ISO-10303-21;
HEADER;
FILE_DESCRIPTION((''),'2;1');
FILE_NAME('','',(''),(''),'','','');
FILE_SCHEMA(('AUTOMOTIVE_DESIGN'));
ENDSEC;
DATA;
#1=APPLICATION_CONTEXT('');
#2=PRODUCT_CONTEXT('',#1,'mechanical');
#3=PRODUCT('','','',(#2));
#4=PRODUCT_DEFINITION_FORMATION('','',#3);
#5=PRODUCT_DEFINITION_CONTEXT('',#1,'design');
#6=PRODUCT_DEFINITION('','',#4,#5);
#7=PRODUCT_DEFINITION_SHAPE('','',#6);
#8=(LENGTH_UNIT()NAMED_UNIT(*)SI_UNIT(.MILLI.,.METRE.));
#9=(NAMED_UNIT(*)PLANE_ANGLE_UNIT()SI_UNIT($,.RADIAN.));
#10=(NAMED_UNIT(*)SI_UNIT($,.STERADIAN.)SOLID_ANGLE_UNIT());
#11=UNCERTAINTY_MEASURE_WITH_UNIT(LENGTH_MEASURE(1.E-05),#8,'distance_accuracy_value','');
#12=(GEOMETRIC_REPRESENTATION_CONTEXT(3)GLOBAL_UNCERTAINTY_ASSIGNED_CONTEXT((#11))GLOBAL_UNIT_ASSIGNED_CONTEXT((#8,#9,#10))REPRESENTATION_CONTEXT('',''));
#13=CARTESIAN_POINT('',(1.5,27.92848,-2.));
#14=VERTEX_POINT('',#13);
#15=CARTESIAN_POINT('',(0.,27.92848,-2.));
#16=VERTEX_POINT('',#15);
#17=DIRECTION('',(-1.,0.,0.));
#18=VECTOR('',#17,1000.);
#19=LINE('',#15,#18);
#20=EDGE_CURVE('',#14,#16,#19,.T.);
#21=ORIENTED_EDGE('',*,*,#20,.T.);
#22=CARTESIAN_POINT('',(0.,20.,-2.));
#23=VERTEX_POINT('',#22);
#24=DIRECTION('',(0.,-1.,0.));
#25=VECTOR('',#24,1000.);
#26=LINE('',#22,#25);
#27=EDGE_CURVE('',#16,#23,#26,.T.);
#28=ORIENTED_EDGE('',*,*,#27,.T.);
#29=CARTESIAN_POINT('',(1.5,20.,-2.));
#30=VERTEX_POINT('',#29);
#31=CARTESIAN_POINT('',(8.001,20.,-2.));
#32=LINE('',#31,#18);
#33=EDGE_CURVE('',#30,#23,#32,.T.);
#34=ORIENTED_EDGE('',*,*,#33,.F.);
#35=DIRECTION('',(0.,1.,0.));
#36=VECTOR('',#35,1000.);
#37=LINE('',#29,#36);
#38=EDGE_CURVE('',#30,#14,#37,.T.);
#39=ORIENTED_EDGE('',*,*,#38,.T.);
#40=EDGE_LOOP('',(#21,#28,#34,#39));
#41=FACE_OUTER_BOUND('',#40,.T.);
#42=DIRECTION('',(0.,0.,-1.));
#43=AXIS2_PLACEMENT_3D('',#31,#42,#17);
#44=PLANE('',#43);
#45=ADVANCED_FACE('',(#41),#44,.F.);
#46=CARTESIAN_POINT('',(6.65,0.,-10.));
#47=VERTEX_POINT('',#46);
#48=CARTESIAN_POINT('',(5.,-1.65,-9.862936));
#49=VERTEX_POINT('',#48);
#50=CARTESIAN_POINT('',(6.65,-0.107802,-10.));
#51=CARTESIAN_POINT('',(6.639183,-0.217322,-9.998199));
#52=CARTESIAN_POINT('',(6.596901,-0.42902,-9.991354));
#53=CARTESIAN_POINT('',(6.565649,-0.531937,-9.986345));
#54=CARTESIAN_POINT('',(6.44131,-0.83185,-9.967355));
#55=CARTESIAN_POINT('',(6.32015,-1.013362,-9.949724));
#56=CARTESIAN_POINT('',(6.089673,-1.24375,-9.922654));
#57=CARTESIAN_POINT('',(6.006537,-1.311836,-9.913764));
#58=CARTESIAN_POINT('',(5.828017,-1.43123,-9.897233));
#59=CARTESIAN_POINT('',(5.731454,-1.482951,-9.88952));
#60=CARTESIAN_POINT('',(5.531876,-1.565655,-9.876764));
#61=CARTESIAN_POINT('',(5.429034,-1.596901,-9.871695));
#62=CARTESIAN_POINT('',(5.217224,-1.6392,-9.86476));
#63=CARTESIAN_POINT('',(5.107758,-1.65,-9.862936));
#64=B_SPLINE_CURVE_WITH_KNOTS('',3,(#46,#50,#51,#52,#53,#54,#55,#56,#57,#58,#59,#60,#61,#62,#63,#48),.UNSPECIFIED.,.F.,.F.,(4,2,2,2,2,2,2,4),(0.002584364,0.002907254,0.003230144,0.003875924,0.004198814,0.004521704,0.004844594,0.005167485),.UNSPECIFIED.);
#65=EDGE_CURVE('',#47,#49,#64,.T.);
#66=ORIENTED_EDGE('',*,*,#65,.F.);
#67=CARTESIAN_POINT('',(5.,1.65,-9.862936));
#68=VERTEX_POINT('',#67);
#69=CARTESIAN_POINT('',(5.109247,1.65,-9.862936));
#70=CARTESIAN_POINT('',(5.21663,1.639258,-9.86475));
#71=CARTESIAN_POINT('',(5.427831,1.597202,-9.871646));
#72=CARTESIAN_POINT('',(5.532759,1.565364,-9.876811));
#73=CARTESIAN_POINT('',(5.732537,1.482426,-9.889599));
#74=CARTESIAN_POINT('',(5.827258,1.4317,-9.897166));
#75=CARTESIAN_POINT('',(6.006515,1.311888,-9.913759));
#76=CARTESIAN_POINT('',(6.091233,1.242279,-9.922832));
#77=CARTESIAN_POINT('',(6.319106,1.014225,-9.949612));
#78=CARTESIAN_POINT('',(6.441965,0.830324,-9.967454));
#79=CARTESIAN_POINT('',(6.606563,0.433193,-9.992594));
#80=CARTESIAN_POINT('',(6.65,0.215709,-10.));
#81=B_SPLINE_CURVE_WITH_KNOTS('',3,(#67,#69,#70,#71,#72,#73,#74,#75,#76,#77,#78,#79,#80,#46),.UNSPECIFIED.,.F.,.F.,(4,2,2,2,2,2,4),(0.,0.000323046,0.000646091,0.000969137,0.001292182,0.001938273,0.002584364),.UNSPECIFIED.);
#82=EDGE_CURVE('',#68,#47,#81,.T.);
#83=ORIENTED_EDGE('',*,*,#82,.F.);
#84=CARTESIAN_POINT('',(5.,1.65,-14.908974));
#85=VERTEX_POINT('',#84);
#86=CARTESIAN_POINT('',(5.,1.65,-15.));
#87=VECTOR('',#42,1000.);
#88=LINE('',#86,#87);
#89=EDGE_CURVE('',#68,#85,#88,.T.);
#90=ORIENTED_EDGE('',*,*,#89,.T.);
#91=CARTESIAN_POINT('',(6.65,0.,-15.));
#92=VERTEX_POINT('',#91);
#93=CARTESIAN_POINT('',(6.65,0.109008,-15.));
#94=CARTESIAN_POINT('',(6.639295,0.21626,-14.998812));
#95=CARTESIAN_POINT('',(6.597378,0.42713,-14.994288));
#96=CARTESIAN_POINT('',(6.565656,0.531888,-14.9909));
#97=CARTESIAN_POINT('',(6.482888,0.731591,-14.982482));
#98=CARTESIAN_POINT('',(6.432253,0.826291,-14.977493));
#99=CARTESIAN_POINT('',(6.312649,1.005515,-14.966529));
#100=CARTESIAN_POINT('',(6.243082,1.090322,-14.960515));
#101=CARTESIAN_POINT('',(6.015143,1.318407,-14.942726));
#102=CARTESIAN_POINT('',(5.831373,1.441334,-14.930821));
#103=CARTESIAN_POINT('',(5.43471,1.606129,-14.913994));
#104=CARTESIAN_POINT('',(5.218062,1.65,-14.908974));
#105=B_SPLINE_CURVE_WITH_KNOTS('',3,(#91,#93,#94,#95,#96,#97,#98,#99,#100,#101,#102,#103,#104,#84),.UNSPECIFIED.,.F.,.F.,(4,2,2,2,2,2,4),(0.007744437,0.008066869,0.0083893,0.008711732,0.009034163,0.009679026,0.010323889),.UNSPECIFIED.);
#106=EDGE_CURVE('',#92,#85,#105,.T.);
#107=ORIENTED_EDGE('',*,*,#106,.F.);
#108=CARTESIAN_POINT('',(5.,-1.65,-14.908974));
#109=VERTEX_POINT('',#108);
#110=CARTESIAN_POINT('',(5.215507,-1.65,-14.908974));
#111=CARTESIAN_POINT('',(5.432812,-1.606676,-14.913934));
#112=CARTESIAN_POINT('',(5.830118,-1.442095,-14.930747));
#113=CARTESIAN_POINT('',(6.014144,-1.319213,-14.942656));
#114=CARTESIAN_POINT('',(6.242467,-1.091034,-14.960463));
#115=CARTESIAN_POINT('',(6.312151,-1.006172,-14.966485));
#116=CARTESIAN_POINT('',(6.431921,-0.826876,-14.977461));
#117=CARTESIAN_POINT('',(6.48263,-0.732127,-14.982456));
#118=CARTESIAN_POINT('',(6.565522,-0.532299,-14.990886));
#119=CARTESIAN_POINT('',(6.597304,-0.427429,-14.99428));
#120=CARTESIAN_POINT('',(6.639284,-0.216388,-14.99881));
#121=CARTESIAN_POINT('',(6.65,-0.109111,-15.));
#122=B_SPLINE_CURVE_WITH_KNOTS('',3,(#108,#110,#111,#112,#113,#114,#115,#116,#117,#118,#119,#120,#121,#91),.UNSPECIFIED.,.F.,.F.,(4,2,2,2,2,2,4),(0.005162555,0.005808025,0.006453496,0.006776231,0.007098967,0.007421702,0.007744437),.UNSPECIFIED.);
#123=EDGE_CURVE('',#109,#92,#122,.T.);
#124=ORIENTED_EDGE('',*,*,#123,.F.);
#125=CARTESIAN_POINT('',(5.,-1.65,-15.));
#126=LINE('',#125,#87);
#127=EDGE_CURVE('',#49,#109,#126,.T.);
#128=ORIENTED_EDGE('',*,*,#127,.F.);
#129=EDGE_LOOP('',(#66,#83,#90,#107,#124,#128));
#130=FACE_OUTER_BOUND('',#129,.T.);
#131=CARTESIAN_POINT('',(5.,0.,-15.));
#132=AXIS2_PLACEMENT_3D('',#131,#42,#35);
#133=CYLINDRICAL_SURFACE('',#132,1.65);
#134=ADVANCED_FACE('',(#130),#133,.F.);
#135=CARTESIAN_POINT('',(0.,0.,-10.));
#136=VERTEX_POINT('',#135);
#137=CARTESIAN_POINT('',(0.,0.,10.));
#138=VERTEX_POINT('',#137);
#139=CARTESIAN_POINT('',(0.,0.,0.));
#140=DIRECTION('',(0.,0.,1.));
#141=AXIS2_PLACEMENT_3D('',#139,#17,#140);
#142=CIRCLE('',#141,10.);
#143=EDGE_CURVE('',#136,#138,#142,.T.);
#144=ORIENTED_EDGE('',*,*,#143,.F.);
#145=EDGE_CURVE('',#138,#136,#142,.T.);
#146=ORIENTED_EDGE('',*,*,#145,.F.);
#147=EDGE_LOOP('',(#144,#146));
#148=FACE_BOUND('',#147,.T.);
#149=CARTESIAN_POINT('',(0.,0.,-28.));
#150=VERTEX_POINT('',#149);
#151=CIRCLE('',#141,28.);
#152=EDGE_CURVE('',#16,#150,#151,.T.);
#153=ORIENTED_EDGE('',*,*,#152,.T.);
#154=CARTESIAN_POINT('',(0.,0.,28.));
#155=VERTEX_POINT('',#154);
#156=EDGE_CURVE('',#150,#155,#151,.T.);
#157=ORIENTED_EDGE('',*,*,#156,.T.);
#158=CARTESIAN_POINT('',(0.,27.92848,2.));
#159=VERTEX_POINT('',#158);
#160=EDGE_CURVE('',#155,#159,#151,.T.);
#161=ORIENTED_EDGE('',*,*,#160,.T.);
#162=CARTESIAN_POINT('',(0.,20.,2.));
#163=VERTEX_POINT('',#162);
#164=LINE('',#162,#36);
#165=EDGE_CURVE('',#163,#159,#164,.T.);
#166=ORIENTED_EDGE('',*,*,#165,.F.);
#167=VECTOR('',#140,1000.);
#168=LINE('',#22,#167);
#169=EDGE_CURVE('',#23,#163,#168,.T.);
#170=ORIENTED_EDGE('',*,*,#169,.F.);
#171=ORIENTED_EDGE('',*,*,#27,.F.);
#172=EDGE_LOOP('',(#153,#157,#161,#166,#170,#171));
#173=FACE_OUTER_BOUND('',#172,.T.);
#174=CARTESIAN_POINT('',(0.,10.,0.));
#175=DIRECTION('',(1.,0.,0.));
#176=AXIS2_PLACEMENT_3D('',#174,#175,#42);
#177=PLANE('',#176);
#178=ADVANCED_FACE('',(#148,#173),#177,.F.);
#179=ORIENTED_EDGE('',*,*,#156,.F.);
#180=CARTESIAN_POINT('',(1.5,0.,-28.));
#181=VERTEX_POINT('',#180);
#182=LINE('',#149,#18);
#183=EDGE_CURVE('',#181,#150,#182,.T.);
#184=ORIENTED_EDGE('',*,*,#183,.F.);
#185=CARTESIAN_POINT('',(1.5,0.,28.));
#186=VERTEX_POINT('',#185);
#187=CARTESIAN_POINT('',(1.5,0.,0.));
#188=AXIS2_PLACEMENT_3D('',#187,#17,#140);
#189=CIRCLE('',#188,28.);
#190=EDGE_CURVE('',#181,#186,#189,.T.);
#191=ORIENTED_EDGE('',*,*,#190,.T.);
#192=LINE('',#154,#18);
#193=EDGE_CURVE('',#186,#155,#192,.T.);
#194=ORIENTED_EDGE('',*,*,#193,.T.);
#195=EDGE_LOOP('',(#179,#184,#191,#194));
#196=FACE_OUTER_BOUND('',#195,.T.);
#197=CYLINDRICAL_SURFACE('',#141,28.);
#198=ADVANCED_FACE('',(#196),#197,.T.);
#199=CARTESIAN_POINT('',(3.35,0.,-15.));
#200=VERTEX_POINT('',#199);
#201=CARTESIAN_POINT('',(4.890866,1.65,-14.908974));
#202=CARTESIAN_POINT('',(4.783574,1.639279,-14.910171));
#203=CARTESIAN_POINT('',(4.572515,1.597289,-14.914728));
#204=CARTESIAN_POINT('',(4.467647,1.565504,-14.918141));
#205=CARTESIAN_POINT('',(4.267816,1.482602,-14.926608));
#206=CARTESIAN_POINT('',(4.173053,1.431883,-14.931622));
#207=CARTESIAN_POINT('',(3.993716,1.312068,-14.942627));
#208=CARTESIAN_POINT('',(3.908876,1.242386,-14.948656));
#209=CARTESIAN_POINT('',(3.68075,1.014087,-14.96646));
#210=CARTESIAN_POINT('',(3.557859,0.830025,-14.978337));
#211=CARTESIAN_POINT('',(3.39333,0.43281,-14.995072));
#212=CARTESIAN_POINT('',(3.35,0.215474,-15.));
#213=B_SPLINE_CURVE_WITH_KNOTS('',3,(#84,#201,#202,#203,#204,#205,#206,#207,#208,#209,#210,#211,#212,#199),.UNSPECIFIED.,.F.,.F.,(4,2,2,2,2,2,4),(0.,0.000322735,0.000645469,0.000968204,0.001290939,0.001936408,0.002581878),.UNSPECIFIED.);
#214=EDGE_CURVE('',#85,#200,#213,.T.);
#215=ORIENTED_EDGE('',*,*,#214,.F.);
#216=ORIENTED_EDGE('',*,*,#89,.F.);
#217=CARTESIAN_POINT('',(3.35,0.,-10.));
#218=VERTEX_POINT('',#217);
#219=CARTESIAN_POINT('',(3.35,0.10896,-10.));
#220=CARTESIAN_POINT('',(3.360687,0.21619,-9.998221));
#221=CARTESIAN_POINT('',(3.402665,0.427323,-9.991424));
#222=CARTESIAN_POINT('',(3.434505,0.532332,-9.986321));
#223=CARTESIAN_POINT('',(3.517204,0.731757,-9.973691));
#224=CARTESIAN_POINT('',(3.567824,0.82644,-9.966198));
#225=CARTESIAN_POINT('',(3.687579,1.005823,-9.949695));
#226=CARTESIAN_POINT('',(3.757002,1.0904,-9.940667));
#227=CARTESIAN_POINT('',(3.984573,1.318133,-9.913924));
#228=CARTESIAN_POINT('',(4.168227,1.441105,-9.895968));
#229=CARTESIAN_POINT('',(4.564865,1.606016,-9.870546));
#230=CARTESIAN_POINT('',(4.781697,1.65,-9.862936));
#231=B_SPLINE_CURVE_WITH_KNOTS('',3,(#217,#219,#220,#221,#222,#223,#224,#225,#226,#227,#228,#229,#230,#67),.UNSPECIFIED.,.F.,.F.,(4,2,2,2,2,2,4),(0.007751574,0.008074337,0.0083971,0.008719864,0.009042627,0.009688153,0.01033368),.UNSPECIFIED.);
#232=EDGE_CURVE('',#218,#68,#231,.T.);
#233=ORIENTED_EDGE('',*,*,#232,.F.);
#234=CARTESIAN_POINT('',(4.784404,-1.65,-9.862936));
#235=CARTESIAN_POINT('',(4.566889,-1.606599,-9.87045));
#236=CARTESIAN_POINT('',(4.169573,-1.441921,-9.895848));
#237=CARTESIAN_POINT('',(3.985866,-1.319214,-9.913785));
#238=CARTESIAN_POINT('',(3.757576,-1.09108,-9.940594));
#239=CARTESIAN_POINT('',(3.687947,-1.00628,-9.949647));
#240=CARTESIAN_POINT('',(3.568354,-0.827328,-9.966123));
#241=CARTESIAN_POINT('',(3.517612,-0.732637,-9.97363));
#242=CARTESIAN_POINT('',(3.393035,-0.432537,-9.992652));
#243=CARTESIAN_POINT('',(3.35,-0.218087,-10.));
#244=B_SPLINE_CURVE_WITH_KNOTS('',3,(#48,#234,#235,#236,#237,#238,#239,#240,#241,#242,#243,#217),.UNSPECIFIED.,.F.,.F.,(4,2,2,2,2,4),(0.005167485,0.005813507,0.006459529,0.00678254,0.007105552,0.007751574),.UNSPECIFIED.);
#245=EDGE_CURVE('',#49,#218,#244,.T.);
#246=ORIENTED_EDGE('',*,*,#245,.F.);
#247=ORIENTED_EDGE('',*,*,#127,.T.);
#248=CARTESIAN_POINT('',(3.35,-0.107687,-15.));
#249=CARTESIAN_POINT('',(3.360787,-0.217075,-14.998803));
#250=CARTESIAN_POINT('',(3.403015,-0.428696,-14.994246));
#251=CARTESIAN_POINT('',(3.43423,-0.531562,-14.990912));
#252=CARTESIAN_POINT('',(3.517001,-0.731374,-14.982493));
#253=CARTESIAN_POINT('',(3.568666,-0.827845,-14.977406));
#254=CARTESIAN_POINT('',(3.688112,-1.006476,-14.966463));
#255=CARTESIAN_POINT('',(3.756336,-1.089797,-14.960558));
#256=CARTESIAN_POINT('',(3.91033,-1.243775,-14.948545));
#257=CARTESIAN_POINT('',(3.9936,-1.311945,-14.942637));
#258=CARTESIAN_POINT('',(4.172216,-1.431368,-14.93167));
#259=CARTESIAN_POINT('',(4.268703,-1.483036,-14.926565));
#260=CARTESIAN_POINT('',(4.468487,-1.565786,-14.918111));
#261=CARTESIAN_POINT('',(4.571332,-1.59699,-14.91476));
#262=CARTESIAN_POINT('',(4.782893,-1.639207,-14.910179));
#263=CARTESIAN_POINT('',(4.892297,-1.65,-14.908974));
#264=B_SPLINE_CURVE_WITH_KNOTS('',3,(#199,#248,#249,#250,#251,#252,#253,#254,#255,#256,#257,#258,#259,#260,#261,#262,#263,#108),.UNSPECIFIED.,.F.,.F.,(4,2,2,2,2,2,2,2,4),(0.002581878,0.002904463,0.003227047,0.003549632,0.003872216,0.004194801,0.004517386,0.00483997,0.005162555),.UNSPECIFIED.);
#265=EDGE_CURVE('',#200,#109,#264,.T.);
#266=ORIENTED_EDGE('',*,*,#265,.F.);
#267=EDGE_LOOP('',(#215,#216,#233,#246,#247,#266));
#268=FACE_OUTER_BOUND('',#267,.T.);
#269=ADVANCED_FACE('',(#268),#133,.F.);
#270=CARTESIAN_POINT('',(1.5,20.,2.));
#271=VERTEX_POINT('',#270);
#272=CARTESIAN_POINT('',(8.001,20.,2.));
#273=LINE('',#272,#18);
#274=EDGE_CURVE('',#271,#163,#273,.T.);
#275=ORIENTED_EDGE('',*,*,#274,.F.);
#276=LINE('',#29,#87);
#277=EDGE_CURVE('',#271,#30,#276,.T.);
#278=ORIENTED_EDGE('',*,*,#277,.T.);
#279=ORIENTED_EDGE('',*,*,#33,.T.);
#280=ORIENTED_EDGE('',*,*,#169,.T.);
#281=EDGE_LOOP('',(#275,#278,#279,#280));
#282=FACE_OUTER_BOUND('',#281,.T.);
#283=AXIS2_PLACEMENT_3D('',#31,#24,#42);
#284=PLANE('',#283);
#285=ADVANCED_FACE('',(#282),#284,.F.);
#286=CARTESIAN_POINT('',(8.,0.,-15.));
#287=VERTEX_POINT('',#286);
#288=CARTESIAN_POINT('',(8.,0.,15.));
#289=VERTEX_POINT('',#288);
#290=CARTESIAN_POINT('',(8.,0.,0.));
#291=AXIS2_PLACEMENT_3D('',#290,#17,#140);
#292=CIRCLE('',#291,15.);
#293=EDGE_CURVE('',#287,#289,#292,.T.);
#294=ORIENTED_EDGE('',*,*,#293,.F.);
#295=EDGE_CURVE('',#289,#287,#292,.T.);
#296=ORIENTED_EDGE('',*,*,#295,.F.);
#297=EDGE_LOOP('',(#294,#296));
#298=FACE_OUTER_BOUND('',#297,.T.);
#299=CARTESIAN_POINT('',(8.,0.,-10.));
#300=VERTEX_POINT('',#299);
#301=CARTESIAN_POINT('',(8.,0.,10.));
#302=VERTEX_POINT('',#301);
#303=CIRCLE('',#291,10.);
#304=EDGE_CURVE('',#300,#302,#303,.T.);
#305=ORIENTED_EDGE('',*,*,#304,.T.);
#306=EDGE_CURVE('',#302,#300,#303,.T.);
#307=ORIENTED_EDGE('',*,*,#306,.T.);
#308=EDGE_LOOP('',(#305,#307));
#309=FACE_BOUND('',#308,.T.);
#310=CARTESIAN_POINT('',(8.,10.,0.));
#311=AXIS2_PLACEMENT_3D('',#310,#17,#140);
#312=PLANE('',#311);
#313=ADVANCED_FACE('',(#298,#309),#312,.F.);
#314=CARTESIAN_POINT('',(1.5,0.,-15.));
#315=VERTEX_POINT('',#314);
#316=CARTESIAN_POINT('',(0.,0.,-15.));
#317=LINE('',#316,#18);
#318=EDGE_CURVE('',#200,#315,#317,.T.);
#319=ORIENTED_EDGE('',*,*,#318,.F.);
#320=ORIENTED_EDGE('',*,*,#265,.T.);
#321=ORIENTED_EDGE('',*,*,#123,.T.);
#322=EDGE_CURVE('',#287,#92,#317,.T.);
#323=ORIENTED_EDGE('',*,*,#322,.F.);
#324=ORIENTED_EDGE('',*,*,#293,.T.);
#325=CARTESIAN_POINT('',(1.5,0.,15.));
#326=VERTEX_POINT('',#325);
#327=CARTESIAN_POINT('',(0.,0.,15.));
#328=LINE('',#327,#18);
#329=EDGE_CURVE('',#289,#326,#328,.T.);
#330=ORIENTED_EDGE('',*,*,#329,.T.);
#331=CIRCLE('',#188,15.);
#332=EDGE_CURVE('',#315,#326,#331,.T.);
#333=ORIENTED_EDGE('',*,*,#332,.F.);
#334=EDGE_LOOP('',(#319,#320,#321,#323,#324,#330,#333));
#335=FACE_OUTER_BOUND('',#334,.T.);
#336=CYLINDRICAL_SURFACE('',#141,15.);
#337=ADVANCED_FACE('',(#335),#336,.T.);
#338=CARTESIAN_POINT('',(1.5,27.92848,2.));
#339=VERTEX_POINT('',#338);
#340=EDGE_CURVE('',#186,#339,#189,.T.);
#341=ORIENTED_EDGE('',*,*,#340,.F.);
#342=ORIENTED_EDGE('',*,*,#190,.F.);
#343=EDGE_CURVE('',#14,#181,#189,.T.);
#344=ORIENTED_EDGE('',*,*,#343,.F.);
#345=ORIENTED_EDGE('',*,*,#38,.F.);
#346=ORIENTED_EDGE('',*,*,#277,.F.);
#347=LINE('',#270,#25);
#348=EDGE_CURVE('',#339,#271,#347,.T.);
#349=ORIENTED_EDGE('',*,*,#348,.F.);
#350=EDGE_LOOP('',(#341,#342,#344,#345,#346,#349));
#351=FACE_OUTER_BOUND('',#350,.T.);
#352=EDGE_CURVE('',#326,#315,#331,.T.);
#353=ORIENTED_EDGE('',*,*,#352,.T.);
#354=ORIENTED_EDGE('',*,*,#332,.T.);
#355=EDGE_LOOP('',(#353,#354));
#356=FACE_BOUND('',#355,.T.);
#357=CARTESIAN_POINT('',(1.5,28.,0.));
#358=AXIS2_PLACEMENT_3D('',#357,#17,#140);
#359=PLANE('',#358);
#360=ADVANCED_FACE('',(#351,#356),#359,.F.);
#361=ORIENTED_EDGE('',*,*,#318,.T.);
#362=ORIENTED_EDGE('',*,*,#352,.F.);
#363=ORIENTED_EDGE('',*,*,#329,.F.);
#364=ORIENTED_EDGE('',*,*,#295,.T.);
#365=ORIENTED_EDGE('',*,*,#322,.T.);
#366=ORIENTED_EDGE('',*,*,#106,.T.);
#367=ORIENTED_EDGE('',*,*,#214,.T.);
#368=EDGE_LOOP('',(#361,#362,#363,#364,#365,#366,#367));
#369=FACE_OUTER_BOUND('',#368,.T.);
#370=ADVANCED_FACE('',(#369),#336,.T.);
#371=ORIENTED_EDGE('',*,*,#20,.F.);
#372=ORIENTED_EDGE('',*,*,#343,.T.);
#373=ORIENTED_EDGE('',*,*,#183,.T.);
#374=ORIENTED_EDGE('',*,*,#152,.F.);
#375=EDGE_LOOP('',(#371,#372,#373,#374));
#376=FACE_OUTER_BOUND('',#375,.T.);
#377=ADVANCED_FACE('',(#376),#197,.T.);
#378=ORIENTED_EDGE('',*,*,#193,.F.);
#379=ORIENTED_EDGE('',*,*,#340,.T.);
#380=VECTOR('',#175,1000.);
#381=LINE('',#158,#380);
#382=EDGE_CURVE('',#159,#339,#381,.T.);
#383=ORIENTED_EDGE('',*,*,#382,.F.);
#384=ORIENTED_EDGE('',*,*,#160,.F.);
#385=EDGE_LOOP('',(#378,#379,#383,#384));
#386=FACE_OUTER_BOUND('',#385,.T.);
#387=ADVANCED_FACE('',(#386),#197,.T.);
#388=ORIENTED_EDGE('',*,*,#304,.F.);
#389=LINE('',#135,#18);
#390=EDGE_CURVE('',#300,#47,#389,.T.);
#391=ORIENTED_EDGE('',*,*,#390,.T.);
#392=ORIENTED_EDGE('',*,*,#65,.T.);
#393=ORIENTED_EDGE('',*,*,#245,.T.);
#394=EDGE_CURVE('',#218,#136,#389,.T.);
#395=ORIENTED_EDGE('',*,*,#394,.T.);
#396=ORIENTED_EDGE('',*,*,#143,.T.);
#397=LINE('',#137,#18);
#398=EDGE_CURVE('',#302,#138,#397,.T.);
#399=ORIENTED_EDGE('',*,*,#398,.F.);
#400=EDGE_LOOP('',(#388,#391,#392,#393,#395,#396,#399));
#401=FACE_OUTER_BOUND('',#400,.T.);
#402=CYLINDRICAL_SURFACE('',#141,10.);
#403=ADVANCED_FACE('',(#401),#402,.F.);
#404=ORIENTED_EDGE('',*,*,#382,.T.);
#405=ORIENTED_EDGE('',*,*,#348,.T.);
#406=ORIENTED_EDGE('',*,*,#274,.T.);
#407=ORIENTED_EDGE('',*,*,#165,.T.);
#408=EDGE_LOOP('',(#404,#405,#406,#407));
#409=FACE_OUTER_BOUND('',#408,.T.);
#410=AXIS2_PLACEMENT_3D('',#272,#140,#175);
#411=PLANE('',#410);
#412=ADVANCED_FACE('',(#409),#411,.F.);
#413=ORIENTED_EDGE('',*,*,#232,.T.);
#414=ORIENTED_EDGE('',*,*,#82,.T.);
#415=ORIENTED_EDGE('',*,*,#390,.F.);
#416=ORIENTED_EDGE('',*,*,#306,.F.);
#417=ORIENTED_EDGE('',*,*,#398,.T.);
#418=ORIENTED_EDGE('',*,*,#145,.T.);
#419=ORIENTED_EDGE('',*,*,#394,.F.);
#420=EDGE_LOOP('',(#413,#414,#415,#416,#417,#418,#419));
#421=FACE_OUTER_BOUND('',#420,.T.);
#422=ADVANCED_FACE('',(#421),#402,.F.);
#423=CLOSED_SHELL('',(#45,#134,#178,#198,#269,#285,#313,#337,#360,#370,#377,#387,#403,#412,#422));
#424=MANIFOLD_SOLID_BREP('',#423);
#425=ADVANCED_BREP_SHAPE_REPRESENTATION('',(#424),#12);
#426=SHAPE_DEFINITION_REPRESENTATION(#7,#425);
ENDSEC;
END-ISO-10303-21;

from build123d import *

# Parameters (mm, degrees)
CUT_EXTRUDE1_REACH     = 42.398
SKETCH2_W              = 4
SKETCH2_H              = 9.816803941
M4_TAPPED_HOLE1_REACH  = 53.556
M4_TAPPED_HOLE1_BORE_R = 1.65


with BuildPart() as part:
    # Sketch1 → Revolve1 (revolve)
    with BuildSketch(Plane.XY, mode=Mode.PRIVATE) as revolve1_sk:
        Polygon((0, 10), (8, 10), (8, 15), (1.5, 15), (1.5, 28), (0, 28), align=None)
    revolve(revolve1_sk.sketch.rotate(Axis((0, 0, 0), (1, 0, 0)), 90), axis=Axis((0, 0, 0), (1, 0, 0)))

    # Sketch2 → Cut-Extrude1 (cut, up to next)
    with BuildSketch(Plane.ZY, mode=Mode.PRIVATE) as cut_extrude1_sk1:
        with Locations((0, 24.908401971)):
            Rectangle(SKETCH2_W, SKETCH2_H)
    cut_extrude1_tool1 = extrude(cut_extrude1_sk1.sketch, amount=-CUT_EXTRUDE1_REACH, mode=Mode.PRIVATE) & part.part
    add(cut_extrude1_tool1.solids().sort_by_distance((0, 24.908402, 0))[0], mode=Mode.SUBTRACT)

    # M4 Tapped Hole1 bore (on position points) → M4 Tapped Hole1 (cut, up to next)
    with BuildSketch(Plane(origin=(5, 0, -15), x_dir=(0, -1, 0), z_dir=(0, 0, -1)), mode=Mode.PRIVATE) as m4_tapped_hole1_sk1:
        Circle(M4_TAPPED_HOLE1_BORE_R)
    m4_tapped_hole1_tool1 = extrude(m4_tapped_hole1_sk1.sketch, amount=-M4_TAPPED_HOLE1_REACH, mode=Mode.PRIVATE) & part.part
    add(m4_tapped_hole1_tool1.solids().sort_by_distance((5, 0, -15))[0], mode=Mode.SUBTRACT)


solid = part.part
